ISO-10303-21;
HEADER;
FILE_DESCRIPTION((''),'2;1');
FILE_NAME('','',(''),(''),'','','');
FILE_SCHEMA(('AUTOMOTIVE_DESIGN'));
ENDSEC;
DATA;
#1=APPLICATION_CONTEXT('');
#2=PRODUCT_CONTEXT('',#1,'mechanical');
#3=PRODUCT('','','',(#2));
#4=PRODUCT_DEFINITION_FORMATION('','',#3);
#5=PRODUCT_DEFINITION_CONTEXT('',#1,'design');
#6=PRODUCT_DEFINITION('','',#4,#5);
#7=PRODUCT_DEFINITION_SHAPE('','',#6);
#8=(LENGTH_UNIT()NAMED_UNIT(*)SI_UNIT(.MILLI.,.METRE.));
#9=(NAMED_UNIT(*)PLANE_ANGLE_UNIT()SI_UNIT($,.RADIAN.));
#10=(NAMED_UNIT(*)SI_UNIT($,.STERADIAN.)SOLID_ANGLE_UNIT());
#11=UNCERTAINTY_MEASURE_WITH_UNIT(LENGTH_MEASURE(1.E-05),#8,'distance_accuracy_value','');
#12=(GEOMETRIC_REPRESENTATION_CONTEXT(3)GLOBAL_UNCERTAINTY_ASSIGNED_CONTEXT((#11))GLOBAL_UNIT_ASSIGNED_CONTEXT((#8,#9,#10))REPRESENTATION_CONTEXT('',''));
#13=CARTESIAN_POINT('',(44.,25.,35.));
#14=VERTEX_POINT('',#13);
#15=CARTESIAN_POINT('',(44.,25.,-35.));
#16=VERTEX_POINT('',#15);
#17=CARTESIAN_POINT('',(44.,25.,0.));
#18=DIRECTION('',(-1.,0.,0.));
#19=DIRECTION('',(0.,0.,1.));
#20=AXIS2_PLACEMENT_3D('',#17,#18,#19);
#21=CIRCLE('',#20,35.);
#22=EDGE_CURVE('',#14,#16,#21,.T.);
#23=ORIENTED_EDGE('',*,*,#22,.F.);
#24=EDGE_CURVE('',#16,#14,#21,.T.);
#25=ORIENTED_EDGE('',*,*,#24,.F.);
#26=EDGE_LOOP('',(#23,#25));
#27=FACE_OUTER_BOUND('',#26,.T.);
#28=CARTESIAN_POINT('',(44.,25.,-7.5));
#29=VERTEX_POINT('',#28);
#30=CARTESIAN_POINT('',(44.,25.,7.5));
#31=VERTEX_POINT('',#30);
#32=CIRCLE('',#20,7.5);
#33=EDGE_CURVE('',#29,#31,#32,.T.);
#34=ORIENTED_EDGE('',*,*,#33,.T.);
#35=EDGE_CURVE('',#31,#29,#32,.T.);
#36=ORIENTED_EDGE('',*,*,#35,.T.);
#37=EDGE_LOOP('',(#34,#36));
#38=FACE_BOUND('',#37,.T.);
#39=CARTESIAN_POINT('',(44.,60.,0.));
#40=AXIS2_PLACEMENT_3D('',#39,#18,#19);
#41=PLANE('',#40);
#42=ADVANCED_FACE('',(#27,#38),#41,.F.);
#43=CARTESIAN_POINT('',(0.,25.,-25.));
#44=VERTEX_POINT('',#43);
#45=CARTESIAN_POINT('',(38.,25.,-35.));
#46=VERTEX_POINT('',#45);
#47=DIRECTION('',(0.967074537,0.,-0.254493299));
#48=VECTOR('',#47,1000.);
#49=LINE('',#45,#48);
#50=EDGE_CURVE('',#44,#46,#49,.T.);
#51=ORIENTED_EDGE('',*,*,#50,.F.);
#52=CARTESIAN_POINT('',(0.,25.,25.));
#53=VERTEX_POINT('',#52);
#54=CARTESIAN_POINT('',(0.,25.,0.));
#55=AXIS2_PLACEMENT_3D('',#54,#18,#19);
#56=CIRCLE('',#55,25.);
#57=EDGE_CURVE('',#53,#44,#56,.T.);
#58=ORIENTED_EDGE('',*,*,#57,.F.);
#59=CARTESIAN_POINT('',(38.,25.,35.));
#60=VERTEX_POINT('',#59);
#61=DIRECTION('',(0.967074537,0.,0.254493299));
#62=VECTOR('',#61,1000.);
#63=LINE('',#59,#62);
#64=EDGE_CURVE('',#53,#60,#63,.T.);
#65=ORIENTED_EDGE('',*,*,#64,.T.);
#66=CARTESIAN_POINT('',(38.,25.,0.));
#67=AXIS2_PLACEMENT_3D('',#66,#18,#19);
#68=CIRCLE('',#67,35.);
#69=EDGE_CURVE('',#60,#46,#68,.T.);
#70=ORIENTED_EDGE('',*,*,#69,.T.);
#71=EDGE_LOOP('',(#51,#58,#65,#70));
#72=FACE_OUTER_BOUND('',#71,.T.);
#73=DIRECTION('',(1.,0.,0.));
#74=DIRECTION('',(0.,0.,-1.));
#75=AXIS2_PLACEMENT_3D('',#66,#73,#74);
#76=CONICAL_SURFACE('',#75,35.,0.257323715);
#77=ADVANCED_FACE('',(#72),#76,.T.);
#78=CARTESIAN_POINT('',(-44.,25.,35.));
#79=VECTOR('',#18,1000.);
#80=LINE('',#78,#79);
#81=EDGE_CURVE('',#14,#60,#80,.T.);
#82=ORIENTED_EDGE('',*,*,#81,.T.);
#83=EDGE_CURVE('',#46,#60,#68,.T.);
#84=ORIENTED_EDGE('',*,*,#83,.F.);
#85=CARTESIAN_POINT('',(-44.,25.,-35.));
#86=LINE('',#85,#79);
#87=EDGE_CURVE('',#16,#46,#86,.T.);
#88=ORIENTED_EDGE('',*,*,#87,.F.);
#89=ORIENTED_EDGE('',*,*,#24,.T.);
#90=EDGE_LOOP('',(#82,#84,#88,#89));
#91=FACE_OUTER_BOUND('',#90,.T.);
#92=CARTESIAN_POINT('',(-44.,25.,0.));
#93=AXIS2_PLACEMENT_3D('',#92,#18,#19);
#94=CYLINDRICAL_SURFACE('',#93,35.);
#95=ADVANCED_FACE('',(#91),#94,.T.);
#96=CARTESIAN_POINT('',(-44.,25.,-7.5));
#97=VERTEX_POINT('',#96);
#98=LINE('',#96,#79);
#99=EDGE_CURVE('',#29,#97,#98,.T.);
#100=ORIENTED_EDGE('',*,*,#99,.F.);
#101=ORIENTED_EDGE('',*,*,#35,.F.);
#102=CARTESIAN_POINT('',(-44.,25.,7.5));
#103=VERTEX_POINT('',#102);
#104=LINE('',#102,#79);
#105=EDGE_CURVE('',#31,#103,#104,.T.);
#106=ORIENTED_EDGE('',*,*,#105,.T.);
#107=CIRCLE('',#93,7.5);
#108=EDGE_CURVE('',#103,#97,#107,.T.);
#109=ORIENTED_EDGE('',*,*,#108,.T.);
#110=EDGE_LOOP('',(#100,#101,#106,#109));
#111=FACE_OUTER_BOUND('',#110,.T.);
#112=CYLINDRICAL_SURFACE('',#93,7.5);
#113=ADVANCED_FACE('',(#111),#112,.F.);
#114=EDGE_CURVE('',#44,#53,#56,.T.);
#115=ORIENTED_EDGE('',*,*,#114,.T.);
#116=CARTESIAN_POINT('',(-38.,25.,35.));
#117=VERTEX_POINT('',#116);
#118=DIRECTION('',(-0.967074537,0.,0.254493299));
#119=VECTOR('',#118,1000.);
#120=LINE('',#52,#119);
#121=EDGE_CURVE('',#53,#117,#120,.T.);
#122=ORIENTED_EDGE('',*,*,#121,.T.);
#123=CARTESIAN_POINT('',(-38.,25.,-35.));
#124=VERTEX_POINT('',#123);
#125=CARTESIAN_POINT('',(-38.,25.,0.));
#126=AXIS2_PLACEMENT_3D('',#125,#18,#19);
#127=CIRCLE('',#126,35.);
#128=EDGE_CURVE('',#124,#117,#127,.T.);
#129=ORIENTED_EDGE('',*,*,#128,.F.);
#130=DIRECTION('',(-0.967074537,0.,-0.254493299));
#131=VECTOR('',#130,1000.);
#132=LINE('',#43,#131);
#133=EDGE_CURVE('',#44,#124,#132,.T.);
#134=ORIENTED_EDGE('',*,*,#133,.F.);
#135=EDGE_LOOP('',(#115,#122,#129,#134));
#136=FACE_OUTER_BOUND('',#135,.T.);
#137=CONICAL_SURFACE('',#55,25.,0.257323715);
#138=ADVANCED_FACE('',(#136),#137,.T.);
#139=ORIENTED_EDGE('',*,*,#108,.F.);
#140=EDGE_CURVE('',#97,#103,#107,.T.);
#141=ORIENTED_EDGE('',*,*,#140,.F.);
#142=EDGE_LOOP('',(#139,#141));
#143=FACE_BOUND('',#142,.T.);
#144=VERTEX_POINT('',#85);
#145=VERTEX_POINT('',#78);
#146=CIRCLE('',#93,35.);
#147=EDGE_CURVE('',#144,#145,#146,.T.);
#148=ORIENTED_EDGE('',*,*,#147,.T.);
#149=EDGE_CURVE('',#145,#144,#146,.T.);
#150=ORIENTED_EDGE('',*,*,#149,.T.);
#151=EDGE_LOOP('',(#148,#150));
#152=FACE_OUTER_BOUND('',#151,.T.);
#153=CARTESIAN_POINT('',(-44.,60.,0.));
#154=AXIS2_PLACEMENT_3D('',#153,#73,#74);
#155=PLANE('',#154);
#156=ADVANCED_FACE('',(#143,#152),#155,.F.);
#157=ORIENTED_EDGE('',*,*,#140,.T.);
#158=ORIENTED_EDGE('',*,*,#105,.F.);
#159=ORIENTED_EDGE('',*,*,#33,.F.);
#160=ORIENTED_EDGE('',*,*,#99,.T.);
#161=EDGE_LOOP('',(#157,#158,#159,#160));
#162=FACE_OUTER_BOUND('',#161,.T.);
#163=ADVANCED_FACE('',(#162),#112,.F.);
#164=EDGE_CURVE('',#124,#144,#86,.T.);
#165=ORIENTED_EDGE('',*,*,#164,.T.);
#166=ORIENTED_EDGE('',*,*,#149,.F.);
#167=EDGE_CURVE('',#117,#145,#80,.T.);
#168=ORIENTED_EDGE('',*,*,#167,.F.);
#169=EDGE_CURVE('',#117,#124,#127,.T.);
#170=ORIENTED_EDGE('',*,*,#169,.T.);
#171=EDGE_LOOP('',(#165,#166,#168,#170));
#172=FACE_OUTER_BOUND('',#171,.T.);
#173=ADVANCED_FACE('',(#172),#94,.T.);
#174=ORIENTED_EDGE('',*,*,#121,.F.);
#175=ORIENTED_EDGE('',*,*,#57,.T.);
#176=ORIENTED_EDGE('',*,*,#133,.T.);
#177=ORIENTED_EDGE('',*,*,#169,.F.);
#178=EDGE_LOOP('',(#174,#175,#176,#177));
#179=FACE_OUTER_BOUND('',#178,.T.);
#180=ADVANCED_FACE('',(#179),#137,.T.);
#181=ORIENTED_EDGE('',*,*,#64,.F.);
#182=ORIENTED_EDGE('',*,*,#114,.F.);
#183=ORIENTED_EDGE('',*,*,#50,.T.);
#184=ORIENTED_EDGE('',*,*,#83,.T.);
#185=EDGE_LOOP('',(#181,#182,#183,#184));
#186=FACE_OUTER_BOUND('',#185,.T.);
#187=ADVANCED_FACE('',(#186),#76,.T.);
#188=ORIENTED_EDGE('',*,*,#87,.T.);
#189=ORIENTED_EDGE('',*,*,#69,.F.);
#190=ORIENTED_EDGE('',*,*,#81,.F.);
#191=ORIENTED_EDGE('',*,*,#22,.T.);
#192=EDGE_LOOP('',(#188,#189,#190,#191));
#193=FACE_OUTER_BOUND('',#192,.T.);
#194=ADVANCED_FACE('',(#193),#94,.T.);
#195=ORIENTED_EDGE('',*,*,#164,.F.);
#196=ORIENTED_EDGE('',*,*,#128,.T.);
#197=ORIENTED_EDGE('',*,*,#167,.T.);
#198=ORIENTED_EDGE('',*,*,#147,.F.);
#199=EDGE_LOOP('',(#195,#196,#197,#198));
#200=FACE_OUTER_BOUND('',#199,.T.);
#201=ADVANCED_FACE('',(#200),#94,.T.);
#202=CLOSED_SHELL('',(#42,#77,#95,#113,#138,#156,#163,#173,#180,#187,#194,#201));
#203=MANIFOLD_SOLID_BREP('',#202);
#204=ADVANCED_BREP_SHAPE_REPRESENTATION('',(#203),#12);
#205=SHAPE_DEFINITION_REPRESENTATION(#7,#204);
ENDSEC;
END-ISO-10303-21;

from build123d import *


with BuildPart() as part:
    # Roller Profile Sketch → Roller Body Revolve (revolve)
    with BuildSketch(Plane.XY, mode=Mode.PRIVATE) as roller_body_revolve_sk:
        Polygon((0, 50), (-38, 60), (-44, 60), (-44, 32.5), (44, 32.5), (44, 60), (38, 60), align=None)
    revolve(roller_body_revolve_sk.sketch.rotate(Axis((-44, 25, 0), (1, 0, 0)), 90), axis=Axis((-44, 25, 0), (1, 0, 0)))


solid = part.part
